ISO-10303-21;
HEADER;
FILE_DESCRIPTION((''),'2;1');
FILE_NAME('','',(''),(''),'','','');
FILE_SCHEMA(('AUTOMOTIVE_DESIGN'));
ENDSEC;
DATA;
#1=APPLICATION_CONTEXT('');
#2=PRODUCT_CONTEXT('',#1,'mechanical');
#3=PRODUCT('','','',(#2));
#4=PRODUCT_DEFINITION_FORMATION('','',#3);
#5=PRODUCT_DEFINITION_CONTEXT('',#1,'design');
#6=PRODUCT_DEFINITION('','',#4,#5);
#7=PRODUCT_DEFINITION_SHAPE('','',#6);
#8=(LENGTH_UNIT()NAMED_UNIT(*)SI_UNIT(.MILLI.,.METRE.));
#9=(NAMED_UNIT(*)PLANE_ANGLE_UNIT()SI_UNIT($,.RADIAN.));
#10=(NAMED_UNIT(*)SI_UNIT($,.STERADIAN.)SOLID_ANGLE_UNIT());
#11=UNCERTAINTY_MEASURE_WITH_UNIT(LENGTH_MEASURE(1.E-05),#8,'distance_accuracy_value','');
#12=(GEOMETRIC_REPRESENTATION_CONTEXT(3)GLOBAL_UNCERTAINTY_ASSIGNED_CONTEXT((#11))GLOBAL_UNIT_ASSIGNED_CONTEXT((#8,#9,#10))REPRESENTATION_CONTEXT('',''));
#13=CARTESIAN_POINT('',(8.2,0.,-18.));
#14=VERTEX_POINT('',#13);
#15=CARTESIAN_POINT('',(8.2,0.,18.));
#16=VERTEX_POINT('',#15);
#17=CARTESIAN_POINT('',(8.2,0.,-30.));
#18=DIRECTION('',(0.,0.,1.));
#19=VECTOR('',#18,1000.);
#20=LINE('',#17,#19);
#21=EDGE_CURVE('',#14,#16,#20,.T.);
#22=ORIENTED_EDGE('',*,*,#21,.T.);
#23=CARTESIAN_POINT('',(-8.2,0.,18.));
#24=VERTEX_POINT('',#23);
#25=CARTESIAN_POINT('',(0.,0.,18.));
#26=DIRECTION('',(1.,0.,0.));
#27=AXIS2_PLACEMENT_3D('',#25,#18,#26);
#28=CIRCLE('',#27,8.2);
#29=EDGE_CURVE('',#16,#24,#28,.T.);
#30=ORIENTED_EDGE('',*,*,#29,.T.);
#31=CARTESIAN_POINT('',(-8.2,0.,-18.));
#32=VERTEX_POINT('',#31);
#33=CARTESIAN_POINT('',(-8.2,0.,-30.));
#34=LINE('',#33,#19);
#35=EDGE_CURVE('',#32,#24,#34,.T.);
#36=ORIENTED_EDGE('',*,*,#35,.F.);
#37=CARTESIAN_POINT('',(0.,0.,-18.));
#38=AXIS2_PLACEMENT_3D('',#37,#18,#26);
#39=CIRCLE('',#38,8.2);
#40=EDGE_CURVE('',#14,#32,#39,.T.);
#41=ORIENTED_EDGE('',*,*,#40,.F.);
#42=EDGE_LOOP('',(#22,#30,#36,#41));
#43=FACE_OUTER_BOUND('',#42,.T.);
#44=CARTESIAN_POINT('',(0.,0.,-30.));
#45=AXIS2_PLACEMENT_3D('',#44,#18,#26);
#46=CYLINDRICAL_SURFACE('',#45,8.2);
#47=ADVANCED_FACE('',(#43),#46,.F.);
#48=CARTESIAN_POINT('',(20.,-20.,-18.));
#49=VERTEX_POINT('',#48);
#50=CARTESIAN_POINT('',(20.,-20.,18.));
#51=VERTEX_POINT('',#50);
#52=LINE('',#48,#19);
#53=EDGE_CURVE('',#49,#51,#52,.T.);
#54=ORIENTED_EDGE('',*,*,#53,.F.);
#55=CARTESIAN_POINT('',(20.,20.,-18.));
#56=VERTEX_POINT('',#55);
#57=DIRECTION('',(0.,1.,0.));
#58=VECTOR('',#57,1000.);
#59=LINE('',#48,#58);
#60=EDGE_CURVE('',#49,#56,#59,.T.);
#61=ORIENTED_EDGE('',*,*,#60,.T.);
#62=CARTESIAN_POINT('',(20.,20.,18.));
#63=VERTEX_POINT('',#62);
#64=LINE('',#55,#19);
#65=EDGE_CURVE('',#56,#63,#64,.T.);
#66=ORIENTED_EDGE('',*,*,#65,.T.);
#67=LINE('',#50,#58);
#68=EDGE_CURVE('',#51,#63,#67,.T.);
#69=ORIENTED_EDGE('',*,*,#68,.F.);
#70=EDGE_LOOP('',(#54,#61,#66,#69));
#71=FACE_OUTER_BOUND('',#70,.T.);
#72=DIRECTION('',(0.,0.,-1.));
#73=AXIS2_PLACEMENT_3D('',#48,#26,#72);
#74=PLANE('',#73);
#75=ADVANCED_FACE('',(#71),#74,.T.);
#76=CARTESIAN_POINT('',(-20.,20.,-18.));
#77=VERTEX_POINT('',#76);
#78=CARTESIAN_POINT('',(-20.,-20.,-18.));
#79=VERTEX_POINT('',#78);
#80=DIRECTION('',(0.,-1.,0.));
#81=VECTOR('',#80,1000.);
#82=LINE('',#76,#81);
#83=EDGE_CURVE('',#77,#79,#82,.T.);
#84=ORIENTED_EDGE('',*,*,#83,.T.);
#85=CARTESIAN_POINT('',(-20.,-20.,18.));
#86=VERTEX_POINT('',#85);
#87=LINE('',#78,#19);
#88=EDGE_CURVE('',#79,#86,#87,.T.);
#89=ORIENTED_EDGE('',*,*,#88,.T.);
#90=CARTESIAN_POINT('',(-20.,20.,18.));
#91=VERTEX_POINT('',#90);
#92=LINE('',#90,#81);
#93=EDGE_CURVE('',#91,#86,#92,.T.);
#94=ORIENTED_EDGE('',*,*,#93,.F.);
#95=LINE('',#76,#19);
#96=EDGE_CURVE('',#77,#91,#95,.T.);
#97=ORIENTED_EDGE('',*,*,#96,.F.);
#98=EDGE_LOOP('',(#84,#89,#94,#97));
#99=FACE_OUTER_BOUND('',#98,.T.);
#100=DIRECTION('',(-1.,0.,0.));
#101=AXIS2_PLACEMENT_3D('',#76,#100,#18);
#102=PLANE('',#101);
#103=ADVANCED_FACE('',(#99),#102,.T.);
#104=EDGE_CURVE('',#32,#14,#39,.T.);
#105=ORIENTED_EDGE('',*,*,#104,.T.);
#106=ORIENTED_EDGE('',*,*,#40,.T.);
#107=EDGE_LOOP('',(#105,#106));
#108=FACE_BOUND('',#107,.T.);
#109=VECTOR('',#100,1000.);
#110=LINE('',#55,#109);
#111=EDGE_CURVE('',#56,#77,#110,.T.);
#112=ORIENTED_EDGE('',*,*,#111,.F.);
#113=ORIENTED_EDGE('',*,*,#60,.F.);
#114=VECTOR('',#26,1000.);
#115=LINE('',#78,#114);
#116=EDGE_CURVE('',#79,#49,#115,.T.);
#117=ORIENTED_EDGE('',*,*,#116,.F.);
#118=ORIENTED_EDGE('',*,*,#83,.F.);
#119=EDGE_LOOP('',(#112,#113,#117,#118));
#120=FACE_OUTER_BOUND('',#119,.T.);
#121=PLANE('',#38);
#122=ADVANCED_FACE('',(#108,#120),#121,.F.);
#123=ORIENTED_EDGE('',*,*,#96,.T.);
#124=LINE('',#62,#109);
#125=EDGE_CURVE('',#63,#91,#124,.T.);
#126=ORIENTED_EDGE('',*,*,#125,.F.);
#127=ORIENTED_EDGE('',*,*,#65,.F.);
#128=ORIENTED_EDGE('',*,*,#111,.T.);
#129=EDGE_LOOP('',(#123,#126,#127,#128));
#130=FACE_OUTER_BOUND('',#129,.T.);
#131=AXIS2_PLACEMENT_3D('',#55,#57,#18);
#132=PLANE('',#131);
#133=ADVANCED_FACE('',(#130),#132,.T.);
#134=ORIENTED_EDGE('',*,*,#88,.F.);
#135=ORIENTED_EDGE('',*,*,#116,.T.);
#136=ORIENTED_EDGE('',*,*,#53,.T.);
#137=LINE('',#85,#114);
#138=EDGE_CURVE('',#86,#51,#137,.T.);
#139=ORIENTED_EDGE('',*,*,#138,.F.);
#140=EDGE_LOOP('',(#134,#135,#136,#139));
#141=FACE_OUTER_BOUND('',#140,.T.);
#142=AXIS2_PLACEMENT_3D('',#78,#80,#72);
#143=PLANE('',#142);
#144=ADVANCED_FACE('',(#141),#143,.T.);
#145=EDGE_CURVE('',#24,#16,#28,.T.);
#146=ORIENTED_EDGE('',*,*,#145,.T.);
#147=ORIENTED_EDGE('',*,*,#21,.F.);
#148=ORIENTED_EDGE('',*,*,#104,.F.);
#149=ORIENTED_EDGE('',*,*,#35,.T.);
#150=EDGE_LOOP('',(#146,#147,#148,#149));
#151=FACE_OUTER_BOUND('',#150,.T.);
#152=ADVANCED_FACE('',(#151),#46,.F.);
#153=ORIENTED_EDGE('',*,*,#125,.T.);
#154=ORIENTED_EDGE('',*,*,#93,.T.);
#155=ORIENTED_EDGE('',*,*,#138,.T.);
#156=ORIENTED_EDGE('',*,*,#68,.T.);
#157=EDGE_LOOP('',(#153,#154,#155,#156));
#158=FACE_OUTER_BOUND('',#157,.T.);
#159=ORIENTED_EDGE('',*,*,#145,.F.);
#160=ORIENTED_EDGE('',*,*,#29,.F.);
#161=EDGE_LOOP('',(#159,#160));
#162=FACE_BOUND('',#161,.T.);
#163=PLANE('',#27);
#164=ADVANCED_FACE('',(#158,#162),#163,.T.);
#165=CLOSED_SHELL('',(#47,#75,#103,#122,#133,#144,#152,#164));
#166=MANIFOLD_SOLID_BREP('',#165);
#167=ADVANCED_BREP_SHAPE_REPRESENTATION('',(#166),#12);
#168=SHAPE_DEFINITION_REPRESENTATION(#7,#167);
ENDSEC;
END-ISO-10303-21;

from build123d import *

# Parameters (mm, degrees)
SKETCH_1_W          = 40
SKETCH_1_H          = 40
EXTRUDE_1_DEPTH     = 18
SKETCH_2_R          = 8.2
CUT_EXTRUDE_1_DEPTH = 30


with BuildPart() as part:
    # 草图1 → 凸台-拉伸1 (new, symmetric)
    with BuildSketch(Plane.XY):
        Rectangle(SKETCH_1_W, SKETCH_1_H)
    extrude(amount=EXTRUDE_1_DEPTH, both=True)

    # 草图2 → 切除-拉伸1 (cut, symmetric)
    with BuildSketch(Plane.XY):
        Circle(SKETCH_2_R)
    extrude(amount=CUT_EXTRUDE_1_DEPTH, both=True, mode=Mode.SUBTRACT)


solid = part.part
